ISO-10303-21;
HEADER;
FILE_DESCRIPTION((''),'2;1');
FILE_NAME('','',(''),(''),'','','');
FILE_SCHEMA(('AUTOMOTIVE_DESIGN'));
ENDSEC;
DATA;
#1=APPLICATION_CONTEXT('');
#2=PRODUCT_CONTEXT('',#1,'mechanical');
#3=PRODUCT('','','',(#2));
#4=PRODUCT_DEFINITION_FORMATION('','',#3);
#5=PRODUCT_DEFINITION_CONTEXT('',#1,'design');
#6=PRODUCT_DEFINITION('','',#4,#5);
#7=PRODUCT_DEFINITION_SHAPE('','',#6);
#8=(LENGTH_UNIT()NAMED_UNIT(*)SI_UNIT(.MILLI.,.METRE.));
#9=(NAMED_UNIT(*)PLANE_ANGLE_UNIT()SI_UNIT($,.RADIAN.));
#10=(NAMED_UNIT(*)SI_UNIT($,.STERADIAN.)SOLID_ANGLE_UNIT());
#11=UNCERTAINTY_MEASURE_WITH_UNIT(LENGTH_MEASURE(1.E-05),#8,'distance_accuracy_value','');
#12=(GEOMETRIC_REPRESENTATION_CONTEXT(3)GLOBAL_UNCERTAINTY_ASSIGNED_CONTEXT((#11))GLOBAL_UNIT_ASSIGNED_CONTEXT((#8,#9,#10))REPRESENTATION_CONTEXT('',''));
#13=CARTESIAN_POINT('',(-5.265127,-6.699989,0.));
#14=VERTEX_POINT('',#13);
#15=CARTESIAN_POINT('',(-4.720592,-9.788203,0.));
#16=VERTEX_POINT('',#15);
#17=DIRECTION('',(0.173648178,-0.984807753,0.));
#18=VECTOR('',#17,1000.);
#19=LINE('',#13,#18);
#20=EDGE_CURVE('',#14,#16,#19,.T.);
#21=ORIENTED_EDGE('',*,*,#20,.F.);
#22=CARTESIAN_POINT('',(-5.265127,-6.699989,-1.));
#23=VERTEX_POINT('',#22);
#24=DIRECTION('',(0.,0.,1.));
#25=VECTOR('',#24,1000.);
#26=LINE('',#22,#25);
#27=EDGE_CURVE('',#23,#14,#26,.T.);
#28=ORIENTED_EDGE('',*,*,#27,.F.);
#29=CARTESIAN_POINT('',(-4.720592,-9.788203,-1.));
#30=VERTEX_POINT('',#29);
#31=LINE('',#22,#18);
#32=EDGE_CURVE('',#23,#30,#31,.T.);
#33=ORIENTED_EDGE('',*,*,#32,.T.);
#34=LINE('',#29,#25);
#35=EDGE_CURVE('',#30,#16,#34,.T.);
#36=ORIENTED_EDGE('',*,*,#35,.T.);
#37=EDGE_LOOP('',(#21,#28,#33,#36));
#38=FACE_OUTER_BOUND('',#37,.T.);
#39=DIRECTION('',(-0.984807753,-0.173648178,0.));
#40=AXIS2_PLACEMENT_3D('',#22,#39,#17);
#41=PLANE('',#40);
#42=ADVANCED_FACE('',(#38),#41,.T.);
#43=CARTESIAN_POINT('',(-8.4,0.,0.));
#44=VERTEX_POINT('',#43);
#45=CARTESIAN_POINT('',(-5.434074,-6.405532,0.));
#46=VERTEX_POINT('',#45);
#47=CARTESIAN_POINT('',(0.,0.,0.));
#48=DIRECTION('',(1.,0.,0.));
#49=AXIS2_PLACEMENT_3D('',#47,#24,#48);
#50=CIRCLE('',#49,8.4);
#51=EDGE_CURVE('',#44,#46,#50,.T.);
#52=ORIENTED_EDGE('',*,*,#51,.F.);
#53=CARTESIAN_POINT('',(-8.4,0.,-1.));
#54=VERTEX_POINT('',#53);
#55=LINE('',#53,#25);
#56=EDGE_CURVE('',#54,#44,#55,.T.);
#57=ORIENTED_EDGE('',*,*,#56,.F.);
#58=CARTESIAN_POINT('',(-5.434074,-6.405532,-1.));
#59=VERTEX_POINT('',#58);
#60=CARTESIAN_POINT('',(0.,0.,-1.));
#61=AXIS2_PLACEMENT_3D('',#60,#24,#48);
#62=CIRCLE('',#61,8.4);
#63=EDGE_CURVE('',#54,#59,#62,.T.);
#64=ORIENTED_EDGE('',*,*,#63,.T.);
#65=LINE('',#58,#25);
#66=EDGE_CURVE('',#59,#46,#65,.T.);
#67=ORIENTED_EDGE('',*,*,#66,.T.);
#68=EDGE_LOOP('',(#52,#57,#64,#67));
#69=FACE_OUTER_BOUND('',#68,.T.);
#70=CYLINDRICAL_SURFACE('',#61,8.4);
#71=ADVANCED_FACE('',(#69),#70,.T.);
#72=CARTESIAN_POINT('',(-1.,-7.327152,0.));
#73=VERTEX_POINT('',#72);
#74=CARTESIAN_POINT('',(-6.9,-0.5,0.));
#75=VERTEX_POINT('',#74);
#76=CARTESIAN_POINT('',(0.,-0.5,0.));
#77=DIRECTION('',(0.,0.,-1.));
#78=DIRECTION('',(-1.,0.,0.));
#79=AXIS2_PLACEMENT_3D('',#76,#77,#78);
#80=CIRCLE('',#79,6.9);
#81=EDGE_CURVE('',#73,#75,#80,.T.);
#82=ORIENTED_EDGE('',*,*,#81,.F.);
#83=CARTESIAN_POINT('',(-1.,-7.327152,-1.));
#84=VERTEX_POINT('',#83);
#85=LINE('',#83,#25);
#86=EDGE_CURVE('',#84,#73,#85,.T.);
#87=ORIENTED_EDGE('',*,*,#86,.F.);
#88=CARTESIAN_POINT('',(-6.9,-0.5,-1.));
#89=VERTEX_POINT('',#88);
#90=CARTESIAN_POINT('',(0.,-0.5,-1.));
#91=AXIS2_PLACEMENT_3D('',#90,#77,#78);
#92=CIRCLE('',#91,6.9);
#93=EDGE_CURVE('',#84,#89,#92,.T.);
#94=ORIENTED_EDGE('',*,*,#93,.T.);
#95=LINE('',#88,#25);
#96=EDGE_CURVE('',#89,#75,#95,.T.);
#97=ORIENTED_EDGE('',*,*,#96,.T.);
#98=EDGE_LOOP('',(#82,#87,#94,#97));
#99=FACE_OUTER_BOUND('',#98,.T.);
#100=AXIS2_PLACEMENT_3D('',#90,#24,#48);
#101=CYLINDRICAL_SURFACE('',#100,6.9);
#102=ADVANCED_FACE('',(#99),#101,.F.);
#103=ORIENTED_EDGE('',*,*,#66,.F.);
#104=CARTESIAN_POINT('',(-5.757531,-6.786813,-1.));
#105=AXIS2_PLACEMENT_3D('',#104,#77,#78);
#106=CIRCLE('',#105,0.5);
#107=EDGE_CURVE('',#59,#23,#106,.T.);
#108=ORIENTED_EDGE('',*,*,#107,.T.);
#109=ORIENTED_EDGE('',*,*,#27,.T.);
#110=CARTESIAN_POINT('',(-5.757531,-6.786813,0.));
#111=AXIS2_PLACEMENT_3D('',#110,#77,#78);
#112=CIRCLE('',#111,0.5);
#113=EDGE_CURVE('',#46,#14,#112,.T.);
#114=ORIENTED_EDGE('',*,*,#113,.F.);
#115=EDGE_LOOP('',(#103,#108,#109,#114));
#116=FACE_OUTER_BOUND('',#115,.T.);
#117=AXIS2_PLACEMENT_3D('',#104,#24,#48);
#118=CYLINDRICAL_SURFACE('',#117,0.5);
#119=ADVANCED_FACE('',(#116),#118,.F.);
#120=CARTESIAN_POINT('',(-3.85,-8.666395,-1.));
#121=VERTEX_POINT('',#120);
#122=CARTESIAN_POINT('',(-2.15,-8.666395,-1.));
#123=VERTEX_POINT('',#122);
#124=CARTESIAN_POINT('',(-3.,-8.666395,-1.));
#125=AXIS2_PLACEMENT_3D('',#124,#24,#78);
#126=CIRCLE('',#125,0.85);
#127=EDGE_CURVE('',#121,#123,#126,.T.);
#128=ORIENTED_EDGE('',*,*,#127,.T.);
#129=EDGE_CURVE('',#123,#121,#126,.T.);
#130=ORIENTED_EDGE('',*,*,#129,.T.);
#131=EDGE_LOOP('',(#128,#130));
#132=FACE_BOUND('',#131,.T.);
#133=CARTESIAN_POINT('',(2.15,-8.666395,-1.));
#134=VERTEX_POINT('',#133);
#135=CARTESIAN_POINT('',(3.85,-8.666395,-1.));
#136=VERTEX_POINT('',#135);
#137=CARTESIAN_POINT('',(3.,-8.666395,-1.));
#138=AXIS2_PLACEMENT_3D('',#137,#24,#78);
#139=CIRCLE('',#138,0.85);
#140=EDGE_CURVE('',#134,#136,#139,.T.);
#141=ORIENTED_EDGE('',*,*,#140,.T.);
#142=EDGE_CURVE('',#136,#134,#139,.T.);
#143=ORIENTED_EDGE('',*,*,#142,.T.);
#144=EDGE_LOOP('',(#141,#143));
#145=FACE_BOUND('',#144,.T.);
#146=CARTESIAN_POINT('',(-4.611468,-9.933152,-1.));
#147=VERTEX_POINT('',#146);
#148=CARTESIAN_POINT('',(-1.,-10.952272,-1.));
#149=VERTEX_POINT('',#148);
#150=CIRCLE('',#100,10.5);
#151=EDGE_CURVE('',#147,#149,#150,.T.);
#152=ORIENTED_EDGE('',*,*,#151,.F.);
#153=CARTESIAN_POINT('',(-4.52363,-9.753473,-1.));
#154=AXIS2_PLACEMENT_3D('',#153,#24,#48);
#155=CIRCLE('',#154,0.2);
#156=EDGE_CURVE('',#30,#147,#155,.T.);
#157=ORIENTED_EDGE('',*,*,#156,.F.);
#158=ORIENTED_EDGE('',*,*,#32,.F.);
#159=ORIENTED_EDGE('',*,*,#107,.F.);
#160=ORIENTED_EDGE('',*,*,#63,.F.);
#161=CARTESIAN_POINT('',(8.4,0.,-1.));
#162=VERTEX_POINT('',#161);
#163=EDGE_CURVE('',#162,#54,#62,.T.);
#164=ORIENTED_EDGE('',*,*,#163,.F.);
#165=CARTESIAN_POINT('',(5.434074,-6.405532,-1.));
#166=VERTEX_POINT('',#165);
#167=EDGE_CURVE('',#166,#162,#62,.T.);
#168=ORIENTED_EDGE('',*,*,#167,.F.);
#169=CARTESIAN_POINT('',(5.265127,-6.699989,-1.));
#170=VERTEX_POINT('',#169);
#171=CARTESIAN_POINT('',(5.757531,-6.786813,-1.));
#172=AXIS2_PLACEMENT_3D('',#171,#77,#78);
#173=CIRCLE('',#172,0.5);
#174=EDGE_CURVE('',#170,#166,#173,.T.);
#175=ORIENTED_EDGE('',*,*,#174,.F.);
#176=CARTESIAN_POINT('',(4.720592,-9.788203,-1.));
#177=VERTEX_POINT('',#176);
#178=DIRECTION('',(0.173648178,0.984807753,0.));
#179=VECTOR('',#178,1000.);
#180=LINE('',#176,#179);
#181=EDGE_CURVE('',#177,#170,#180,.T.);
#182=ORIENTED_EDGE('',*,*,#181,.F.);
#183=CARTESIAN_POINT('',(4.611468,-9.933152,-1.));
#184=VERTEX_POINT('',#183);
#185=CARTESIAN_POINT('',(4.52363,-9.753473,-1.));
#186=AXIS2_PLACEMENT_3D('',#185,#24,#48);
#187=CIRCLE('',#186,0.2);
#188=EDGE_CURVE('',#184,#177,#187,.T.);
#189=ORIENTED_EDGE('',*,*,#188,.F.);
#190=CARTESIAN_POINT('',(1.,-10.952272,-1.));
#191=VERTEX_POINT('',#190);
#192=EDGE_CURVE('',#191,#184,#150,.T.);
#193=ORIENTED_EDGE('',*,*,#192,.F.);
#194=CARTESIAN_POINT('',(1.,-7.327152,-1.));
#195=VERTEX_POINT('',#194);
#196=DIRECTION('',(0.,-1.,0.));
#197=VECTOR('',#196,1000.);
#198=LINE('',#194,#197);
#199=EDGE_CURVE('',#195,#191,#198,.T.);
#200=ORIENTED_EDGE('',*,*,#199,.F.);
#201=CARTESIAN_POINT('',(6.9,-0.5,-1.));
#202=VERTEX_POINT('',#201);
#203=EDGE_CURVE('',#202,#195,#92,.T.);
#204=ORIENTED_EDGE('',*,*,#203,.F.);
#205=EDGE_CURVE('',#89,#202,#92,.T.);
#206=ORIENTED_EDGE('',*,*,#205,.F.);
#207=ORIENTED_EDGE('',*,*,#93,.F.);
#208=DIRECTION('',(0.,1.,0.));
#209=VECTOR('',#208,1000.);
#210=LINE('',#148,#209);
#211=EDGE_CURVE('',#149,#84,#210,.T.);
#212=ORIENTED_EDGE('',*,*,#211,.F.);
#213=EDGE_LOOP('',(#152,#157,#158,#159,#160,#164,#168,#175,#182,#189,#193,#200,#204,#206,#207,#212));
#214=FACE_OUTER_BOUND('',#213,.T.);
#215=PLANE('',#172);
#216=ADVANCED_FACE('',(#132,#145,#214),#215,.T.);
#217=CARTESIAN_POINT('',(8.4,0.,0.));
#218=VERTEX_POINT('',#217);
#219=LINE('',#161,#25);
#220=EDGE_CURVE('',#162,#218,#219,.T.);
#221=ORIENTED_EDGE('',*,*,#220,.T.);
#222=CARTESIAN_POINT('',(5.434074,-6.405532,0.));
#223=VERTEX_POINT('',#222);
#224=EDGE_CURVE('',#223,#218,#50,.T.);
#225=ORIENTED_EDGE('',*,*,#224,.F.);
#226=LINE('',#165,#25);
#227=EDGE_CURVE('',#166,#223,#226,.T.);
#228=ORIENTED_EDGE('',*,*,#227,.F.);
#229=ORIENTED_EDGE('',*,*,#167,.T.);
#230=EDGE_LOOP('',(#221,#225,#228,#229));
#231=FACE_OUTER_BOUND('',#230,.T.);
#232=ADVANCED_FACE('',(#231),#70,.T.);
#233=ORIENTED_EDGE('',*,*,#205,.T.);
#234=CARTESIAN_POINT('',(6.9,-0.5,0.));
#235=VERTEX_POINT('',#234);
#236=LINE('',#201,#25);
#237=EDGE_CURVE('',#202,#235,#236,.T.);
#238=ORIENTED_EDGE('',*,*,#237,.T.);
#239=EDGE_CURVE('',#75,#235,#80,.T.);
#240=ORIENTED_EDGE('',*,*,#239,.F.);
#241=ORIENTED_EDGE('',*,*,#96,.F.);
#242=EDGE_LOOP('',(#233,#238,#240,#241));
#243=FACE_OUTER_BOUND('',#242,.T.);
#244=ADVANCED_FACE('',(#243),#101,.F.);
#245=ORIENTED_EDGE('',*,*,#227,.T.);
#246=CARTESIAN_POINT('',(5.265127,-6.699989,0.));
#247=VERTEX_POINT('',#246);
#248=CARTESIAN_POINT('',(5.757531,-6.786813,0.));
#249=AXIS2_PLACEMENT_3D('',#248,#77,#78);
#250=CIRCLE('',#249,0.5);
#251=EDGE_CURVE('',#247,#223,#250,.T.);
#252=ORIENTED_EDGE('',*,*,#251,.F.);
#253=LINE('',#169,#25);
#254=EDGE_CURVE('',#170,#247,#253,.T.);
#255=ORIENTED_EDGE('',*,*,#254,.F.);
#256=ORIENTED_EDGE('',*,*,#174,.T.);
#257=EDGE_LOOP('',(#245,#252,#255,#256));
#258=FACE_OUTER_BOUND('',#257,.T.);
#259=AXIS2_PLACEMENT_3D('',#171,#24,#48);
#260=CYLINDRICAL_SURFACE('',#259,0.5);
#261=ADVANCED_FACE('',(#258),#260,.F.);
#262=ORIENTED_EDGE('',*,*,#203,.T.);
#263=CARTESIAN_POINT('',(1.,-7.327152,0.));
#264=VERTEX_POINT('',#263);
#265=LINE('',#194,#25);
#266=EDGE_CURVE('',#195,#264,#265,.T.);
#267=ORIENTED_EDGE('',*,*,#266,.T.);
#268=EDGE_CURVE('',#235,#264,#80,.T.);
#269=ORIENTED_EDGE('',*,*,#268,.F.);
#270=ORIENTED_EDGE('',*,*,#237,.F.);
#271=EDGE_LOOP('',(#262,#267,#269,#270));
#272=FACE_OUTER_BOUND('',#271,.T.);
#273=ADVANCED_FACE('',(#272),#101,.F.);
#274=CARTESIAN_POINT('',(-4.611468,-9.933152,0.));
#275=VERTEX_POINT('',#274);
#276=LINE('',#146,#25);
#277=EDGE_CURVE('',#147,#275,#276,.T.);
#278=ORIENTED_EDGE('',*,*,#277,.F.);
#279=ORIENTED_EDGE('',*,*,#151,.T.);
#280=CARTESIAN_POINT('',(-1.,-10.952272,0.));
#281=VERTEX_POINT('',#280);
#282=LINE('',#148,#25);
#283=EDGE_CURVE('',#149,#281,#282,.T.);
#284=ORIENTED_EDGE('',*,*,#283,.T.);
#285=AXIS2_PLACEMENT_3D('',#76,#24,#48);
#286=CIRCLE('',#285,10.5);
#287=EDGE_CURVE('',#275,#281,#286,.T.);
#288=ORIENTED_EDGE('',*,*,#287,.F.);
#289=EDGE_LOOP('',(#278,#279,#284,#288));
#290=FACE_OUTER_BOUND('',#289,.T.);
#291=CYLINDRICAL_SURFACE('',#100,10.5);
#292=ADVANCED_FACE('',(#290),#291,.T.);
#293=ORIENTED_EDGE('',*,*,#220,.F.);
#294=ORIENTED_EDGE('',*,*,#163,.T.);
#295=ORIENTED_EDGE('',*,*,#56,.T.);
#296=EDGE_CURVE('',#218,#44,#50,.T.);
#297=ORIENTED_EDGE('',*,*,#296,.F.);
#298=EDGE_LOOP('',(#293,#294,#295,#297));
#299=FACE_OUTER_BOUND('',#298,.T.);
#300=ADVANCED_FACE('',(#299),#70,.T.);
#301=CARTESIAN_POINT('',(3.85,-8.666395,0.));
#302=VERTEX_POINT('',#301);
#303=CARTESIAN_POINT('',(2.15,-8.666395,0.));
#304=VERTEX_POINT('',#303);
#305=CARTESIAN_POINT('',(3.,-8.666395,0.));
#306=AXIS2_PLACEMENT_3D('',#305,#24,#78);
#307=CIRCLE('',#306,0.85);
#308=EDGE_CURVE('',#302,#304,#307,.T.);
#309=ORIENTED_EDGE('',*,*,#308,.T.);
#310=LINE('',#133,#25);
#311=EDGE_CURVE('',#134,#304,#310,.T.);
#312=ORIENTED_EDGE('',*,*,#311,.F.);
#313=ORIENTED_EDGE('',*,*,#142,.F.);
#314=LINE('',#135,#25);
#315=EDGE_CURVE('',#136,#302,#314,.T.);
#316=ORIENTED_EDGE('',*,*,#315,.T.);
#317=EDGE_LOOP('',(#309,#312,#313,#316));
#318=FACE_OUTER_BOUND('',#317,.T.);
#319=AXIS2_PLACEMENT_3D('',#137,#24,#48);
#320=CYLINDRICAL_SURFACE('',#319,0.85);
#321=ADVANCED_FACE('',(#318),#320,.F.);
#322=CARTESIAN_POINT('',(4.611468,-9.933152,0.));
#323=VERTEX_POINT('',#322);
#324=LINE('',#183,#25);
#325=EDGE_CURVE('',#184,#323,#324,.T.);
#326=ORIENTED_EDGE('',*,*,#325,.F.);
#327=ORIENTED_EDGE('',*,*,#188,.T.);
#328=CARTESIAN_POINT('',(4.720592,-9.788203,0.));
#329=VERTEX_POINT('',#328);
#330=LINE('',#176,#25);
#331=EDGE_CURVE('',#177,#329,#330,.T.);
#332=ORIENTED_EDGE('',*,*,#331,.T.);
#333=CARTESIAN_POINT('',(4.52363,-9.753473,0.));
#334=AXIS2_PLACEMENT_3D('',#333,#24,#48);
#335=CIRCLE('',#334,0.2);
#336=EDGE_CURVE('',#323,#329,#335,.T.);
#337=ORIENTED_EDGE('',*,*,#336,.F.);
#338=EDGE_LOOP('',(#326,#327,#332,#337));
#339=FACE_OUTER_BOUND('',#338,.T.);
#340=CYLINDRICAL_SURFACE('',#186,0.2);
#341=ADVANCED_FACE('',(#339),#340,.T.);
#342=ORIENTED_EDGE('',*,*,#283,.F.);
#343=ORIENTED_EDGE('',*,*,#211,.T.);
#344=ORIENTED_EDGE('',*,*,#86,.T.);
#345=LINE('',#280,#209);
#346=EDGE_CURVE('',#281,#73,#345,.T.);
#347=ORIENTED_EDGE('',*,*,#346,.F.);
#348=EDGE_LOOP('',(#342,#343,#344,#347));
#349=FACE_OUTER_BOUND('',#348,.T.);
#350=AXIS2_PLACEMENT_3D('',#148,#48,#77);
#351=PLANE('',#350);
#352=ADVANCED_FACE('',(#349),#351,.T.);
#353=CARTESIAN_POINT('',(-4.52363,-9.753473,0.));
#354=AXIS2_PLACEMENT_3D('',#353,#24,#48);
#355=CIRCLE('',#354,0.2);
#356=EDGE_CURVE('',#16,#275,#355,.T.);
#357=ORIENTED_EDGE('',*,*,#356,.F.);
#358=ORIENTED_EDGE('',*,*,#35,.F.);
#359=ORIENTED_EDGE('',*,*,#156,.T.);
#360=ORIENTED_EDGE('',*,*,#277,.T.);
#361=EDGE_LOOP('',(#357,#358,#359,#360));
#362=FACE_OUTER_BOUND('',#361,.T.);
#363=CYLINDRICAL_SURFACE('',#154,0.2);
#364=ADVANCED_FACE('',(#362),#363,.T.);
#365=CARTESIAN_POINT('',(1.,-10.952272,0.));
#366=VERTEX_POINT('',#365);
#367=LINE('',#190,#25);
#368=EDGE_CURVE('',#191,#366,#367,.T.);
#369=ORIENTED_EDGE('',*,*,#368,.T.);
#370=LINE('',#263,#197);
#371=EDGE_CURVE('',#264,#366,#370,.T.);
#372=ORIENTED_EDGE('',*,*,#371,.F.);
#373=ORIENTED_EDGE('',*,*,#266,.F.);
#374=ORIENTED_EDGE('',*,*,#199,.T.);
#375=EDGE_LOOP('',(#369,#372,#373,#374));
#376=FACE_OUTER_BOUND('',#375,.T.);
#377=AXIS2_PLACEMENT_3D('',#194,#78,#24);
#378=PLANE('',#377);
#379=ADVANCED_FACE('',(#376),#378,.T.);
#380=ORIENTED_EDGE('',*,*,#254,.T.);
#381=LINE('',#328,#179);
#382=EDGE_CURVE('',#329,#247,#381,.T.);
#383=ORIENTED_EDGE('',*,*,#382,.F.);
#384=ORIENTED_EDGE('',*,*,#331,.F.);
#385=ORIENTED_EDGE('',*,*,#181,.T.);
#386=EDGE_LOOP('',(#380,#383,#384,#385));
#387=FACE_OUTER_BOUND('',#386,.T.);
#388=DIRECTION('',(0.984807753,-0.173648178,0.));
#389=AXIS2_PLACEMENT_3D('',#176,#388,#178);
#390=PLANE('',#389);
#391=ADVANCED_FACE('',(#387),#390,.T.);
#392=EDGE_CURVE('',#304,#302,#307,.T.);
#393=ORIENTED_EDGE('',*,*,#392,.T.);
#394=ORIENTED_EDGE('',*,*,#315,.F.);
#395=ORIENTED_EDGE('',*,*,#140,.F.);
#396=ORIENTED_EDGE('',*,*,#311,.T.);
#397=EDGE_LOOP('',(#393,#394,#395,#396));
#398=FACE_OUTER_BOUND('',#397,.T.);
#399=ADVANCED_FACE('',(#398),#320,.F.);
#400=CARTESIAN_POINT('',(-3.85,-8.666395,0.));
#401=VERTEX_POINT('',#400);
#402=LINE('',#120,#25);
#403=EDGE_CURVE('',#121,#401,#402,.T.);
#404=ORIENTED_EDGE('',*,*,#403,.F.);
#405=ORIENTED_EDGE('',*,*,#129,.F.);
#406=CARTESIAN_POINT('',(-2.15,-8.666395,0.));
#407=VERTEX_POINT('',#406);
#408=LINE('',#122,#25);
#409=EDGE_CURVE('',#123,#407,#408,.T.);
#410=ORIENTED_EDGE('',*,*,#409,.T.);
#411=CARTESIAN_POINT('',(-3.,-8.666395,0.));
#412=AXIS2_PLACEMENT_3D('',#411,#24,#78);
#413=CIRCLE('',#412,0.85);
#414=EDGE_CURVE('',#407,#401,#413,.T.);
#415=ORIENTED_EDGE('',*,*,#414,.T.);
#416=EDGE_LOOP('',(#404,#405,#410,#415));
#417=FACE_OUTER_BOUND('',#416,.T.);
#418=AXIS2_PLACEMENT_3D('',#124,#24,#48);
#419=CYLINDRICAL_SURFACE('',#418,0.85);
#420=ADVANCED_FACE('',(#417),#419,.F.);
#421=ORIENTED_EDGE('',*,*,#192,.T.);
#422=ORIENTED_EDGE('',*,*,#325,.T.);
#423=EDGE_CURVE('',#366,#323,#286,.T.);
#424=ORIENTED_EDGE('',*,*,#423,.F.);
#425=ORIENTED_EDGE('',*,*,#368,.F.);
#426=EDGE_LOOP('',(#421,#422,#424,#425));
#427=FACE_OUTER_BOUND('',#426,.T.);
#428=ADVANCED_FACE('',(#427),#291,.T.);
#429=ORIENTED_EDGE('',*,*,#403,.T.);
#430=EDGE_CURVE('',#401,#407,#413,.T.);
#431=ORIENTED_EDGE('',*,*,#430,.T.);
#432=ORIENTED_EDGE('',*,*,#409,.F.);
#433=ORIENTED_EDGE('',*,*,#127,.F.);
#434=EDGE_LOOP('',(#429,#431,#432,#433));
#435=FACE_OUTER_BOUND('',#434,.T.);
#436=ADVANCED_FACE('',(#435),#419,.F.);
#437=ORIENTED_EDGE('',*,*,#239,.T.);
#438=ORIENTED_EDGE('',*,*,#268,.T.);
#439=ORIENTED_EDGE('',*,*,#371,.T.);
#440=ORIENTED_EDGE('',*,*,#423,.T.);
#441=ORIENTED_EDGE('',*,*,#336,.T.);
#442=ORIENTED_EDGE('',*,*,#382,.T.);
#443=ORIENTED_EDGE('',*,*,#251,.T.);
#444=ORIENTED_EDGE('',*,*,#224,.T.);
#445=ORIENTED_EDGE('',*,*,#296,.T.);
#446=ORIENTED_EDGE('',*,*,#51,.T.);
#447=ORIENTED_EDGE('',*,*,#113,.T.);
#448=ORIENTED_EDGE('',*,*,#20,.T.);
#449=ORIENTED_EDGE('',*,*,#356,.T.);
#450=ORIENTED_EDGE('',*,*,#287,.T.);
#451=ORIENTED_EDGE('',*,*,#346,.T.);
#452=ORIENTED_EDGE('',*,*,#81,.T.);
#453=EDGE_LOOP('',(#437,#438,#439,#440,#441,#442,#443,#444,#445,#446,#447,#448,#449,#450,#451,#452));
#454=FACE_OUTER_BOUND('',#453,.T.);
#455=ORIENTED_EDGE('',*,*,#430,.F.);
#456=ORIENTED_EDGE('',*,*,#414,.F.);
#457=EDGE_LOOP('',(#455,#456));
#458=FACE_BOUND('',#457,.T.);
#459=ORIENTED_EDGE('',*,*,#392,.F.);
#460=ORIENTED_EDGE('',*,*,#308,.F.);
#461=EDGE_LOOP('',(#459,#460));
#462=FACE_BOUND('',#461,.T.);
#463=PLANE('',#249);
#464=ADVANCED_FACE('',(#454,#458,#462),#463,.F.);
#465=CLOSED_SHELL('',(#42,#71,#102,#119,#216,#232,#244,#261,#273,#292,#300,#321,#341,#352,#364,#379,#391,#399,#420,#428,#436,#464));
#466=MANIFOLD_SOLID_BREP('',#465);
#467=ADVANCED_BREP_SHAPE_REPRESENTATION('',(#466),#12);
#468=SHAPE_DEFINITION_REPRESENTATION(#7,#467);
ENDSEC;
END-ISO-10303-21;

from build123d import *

# Parameters (mm, degrees)
SKETCH_1_R      = 0.85
EXTRUDE_1_DEPTH = 1


with BuildPart() as part:
    # 草图1 → 凸台-拉伸1 (new body)
    with BuildSketch(Plane.XY):
        with BuildLine():
            Line((-5.265127147, -6.69998934), (-4.720591752, -9.788203027))
            ThreePointArc((-4.720591752, -9.788203027), (-4.683411954, -9.873763838), (-4.611467681, -9.933152486))
            ThreePointArc((-4.611467681, -9.933152486), (-2.851630021, -10.605355324), (-1, -10.95227248))
            Line((-1, -10.95227248), (-1, -7.327151675))
            ThreePointArc((-1, -7.327151675), (0, 6.4), (1, -7.327151675))
            Line((1, -7.327151675), (1, -10.95227248))
            ThreePointArc((1, -10.95227248), (2.851630021, -10.605355324), (4.611467681, -9.933152486))
            ThreePointArc((4.611467681, -9.933152486), (4.683411954, -9.873763838), (4.720591752, -9.788203027))
            Line((4.720591752, -9.788203027), (5.265127147, -6.69998934))
            ThreePointArc((5.265127147, -6.69998934), (5.323845106, -6.537983114), (5.434074225, -6.405531775))
            ThreePointArc((5.434074225, -6.405531775), (0, 8.4), (-5.434074225, -6.405531775))
            ThreePointArc((-5.434074225, -6.405531775), (-5.323845106, -6.537983114), (-5.265127147, -6.69998934))
        make_face()
        with Locations(Location((3, -8.666394553, 0), (0, 0, 180))):
            Circle(SKETCH_1_R, mode=Mode.SUBTRACT)
        with Locations(Location((-3, -8.666394553, 0), (0, 0, 180))):
            Circle(SKETCH_1_R, mode=Mode.SUBTRACT)
    extrude(amount=-EXTRUDE_1_DEPTH)


solid = part.part
